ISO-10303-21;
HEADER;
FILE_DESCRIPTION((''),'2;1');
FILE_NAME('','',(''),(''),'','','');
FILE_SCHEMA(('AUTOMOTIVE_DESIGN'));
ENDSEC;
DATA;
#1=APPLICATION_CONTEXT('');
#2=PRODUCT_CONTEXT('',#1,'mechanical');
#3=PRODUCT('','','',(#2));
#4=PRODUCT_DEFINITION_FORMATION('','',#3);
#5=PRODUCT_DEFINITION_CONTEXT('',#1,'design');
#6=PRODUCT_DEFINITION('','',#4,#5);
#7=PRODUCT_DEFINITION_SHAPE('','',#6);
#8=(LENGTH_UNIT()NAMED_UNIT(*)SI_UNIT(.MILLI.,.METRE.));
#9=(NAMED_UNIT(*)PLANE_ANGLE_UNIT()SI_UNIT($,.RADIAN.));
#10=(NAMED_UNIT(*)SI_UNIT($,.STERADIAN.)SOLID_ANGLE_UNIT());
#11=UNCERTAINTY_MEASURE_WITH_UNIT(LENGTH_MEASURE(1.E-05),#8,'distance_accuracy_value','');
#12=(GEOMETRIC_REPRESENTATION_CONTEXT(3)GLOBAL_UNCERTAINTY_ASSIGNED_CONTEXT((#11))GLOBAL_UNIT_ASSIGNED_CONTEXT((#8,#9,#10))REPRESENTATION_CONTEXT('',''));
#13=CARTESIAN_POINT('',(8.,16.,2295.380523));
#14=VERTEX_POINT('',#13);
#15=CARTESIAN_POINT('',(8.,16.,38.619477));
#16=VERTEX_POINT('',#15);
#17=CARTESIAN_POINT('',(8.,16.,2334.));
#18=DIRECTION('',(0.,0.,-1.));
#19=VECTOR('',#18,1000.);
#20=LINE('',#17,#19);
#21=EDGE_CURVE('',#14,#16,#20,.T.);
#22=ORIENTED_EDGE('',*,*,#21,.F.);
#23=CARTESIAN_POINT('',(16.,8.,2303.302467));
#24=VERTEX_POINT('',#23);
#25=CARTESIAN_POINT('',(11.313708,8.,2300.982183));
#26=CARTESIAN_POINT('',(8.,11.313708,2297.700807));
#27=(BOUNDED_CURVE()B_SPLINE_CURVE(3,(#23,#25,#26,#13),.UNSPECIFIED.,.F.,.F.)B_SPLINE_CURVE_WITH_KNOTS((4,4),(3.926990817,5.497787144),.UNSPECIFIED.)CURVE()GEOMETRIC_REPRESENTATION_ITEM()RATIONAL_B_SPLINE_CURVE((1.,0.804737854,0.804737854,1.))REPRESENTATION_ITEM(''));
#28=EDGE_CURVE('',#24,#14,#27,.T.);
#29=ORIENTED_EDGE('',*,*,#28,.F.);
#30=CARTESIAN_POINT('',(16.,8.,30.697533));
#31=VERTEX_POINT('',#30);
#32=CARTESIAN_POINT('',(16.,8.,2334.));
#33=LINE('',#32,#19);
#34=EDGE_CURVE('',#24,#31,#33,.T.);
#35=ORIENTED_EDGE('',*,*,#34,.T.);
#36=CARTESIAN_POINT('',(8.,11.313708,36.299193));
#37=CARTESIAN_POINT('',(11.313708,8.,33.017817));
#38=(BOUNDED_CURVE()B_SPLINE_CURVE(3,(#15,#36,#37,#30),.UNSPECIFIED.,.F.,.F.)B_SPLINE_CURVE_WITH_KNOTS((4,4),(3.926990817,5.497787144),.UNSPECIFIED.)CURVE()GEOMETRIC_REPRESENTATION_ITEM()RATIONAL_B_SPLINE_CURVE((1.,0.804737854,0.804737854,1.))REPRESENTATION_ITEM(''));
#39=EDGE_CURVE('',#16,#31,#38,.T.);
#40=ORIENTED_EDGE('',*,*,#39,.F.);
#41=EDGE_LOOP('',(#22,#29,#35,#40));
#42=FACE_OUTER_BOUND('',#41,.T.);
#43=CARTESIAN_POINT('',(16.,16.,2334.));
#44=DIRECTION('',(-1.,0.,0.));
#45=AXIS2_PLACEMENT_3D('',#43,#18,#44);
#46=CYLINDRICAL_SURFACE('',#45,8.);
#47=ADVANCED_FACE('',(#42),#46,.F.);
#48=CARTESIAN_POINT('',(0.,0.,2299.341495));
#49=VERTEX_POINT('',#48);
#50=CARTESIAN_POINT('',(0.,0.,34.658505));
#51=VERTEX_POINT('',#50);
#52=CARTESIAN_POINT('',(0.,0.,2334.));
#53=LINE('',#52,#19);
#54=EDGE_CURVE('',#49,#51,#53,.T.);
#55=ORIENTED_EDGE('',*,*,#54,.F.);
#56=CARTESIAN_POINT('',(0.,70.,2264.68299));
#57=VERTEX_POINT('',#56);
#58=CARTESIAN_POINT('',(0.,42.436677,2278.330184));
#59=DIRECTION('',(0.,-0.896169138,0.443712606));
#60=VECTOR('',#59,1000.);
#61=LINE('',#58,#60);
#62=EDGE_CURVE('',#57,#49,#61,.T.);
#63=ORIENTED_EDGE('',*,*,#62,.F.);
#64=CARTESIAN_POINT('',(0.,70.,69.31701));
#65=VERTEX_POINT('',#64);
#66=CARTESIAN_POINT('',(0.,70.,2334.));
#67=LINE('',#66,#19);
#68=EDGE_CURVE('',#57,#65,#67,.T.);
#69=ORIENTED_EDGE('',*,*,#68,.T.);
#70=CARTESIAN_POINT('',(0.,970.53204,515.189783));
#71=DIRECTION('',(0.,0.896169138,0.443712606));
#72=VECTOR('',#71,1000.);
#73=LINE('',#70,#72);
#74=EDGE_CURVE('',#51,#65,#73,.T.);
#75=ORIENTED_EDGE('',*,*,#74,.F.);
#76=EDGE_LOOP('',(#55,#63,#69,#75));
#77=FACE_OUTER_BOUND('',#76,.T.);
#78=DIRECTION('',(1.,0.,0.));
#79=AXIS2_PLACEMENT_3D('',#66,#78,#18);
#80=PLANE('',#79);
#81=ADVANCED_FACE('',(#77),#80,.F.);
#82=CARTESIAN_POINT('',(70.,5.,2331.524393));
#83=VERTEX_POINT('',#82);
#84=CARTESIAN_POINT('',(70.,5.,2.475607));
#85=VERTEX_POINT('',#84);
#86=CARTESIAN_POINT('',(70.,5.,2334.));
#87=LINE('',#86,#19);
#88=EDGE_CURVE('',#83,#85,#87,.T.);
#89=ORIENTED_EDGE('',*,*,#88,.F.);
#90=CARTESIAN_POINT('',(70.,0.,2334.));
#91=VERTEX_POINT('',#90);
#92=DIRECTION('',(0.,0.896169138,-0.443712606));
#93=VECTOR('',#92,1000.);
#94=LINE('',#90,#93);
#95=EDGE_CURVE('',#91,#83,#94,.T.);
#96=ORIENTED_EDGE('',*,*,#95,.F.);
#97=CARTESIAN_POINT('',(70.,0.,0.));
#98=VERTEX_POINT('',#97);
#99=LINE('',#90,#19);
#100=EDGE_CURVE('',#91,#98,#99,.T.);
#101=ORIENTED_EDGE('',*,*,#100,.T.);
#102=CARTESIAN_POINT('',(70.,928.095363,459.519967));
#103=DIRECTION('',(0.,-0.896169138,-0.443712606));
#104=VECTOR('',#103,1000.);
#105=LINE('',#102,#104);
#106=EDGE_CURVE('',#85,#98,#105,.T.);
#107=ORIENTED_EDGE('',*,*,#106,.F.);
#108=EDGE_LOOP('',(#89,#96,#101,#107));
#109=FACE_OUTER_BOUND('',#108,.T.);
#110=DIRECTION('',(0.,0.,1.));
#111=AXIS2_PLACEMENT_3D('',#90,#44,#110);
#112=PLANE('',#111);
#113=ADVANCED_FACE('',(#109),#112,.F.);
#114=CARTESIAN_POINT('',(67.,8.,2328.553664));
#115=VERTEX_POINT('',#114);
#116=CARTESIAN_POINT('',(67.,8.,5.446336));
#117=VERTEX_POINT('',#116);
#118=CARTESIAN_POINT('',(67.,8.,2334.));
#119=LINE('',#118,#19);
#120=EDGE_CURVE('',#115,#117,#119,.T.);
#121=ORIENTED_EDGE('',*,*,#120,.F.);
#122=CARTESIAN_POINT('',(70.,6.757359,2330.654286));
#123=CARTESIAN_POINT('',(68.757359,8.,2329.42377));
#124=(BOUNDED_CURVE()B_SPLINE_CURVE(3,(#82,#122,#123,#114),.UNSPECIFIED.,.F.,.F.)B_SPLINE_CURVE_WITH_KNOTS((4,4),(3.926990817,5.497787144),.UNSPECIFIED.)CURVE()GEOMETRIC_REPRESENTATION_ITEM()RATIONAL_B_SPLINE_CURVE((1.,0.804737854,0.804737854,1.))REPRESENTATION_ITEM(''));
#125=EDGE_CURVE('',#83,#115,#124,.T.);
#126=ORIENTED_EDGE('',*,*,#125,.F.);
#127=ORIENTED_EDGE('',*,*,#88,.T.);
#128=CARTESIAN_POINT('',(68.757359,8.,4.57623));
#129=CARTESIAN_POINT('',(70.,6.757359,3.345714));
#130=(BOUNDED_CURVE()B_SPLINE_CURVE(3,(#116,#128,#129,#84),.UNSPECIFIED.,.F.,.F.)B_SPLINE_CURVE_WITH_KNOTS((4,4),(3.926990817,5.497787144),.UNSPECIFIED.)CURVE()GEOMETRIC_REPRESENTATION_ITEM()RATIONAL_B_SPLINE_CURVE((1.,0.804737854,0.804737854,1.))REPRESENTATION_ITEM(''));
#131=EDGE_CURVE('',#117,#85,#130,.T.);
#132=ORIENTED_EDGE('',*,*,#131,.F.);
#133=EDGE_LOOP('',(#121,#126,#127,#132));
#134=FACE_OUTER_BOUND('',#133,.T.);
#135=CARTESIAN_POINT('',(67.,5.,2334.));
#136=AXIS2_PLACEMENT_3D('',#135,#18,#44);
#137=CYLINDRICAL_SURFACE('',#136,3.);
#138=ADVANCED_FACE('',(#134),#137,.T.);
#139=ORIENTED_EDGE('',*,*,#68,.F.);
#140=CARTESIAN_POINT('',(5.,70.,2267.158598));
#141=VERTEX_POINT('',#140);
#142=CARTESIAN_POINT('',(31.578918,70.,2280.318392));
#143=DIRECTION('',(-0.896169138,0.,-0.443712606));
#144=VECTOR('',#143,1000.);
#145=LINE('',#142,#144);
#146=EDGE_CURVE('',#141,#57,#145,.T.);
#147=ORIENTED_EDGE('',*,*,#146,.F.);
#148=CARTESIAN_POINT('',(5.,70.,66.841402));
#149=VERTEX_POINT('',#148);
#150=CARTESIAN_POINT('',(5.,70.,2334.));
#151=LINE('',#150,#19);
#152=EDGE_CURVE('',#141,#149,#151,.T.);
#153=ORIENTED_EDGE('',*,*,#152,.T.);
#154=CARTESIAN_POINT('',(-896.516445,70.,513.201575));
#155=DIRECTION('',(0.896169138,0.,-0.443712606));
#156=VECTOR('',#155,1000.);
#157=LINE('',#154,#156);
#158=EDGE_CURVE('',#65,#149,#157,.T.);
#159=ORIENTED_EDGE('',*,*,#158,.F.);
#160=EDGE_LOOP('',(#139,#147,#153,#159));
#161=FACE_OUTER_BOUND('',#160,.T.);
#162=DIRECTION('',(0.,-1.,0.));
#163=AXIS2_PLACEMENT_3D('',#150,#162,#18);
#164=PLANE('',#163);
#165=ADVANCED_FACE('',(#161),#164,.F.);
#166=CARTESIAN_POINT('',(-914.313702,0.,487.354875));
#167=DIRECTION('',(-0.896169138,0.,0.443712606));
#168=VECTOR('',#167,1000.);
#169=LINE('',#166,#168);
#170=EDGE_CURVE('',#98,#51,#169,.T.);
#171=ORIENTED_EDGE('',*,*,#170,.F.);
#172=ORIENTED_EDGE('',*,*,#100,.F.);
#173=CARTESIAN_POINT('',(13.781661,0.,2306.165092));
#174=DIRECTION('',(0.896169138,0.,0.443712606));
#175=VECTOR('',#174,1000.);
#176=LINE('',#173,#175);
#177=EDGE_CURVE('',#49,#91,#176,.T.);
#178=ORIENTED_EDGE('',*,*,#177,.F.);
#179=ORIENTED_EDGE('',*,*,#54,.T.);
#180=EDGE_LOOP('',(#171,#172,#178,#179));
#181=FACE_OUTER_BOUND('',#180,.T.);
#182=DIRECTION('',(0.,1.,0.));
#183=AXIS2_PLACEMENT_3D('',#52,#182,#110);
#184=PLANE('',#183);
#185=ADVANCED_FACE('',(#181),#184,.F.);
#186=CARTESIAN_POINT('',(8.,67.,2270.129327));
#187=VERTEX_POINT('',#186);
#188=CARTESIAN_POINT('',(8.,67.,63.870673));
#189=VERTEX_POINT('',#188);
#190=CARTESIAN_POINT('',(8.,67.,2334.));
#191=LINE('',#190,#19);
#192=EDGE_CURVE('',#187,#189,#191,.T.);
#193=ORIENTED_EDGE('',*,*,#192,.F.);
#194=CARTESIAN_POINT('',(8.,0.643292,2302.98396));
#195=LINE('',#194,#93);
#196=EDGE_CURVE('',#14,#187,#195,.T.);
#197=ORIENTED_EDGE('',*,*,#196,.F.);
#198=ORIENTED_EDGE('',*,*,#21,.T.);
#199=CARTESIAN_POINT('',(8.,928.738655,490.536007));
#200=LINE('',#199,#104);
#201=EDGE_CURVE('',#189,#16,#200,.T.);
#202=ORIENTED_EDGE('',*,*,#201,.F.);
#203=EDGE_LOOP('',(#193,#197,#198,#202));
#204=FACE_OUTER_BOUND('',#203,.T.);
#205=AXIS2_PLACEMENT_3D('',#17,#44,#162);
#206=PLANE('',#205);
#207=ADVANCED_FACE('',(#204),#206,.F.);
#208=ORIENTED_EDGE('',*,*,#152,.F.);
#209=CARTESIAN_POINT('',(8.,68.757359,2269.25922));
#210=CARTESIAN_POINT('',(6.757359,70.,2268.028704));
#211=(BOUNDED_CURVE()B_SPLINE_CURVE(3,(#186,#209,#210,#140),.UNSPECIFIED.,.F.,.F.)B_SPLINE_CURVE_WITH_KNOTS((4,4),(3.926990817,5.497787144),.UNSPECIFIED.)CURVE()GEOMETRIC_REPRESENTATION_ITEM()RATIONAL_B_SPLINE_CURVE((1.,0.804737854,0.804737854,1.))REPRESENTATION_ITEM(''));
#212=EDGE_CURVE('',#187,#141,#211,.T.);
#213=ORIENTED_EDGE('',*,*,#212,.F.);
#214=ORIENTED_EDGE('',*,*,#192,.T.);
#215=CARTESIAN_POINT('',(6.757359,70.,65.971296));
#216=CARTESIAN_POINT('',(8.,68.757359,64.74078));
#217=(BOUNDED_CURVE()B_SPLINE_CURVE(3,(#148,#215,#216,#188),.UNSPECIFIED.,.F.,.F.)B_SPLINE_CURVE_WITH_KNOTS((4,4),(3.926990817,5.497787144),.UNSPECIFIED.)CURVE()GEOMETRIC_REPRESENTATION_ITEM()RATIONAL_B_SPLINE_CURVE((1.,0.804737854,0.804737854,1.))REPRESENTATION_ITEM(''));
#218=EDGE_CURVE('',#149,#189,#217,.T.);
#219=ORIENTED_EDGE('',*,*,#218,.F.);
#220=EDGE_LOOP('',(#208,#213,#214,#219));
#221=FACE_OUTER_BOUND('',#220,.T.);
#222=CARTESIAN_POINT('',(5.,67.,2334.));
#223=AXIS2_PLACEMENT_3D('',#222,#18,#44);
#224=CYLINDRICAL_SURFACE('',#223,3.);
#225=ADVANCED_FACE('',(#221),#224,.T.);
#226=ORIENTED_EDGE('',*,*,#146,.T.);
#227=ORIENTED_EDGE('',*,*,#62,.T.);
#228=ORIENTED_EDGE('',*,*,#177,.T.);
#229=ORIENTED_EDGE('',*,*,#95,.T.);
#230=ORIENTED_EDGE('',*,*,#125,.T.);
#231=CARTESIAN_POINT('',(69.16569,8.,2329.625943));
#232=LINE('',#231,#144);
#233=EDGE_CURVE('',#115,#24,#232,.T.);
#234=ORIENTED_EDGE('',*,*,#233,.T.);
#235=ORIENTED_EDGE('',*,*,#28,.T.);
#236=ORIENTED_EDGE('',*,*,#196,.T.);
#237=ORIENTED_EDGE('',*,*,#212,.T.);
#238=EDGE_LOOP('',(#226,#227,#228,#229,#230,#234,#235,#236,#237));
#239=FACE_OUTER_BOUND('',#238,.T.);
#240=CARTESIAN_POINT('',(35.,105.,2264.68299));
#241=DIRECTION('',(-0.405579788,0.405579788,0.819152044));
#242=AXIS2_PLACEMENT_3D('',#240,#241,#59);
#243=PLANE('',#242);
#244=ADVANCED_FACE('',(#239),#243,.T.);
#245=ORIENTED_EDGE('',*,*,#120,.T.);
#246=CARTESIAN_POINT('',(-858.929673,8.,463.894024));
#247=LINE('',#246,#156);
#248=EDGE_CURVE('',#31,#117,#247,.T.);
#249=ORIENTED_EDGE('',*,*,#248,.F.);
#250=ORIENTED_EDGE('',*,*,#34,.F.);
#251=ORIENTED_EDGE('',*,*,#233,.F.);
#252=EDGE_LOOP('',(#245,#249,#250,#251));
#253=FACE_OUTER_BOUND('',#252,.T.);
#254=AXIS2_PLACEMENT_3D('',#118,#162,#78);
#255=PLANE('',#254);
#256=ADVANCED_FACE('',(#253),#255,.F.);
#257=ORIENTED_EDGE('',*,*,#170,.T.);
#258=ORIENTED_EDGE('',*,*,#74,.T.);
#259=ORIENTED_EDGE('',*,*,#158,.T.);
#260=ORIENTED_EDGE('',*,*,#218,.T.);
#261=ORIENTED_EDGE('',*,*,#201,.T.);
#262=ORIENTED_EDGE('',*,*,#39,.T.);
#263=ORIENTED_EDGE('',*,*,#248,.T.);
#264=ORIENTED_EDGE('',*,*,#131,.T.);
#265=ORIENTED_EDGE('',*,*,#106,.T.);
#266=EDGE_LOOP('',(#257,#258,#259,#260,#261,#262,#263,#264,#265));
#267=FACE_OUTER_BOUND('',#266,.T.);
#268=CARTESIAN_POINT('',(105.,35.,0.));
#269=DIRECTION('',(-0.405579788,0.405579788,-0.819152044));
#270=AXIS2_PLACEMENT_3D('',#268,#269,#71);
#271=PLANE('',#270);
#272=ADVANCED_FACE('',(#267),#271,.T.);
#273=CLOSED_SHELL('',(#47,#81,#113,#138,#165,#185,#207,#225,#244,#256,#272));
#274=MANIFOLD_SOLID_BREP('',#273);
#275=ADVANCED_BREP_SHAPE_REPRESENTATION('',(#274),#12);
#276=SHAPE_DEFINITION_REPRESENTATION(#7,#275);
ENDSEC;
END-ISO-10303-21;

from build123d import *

# Parameters (mm, degrees)
BOSS_EXTRUDE1_DEPTH     = 2334
CUT_EXTRUDE4_DEPTH      = 2337.098456829
CUT_EXTRUDE4_DEPTH_BACK = 10


with BuildPart() as part:
    # Sketch1 → Boss-Extrude1 (new body)
    with BuildSketch(Plane.XY):
        with BuildLine():
            Line((0, 70), (0, 0))
            Line((0, 0), (70, 0))
            Line((70, 0), (70, 5))
            ThreePointArc((70, 5), (69.121320344, 7.121320344), (67, 8))
            Line((67, 8), (16, 8))
            ThreePointArc((16, 8), (10.343145751, 10.343145751), (8, 16))
            Line((8, 16), (8, 67))
            ThreePointArc((8, 67), (7.121320344, 69.121320344), (5, 70))
            Line((5, 70), (0, 70))
        make_face()
    extrude(amount=BOSS_EXTRUDE1_DEPTH)

    # Sketch3 → Cut-Extrude4 (cut, two sides: drawn at the far end of the back side and taken through both)
    with BuildSketch(Plane(origin=(0, 0, 0), x_dir=(0, 0, -1), z_dir=(0.7071067811865488, 0.7071067811865464, 0)).offset(-CUT_EXTRUDE4_DEPTH_BACK)):
        Polygon((0, -49.497474683), (-69.317009791, 49.497474683), (0, 49.497474683), align=None)
        Polygon((-2334, -49.497474683), (-2334, 49.497474683), (-2264.682990209, 49.497474683), align=None)
    extrude(amount=CUT_EXTRUDE4_DEPTH + CUT_EXTRUDE4_DEPTH_BACK, mode=Mode.SUBTRACT)


solid = part.part
